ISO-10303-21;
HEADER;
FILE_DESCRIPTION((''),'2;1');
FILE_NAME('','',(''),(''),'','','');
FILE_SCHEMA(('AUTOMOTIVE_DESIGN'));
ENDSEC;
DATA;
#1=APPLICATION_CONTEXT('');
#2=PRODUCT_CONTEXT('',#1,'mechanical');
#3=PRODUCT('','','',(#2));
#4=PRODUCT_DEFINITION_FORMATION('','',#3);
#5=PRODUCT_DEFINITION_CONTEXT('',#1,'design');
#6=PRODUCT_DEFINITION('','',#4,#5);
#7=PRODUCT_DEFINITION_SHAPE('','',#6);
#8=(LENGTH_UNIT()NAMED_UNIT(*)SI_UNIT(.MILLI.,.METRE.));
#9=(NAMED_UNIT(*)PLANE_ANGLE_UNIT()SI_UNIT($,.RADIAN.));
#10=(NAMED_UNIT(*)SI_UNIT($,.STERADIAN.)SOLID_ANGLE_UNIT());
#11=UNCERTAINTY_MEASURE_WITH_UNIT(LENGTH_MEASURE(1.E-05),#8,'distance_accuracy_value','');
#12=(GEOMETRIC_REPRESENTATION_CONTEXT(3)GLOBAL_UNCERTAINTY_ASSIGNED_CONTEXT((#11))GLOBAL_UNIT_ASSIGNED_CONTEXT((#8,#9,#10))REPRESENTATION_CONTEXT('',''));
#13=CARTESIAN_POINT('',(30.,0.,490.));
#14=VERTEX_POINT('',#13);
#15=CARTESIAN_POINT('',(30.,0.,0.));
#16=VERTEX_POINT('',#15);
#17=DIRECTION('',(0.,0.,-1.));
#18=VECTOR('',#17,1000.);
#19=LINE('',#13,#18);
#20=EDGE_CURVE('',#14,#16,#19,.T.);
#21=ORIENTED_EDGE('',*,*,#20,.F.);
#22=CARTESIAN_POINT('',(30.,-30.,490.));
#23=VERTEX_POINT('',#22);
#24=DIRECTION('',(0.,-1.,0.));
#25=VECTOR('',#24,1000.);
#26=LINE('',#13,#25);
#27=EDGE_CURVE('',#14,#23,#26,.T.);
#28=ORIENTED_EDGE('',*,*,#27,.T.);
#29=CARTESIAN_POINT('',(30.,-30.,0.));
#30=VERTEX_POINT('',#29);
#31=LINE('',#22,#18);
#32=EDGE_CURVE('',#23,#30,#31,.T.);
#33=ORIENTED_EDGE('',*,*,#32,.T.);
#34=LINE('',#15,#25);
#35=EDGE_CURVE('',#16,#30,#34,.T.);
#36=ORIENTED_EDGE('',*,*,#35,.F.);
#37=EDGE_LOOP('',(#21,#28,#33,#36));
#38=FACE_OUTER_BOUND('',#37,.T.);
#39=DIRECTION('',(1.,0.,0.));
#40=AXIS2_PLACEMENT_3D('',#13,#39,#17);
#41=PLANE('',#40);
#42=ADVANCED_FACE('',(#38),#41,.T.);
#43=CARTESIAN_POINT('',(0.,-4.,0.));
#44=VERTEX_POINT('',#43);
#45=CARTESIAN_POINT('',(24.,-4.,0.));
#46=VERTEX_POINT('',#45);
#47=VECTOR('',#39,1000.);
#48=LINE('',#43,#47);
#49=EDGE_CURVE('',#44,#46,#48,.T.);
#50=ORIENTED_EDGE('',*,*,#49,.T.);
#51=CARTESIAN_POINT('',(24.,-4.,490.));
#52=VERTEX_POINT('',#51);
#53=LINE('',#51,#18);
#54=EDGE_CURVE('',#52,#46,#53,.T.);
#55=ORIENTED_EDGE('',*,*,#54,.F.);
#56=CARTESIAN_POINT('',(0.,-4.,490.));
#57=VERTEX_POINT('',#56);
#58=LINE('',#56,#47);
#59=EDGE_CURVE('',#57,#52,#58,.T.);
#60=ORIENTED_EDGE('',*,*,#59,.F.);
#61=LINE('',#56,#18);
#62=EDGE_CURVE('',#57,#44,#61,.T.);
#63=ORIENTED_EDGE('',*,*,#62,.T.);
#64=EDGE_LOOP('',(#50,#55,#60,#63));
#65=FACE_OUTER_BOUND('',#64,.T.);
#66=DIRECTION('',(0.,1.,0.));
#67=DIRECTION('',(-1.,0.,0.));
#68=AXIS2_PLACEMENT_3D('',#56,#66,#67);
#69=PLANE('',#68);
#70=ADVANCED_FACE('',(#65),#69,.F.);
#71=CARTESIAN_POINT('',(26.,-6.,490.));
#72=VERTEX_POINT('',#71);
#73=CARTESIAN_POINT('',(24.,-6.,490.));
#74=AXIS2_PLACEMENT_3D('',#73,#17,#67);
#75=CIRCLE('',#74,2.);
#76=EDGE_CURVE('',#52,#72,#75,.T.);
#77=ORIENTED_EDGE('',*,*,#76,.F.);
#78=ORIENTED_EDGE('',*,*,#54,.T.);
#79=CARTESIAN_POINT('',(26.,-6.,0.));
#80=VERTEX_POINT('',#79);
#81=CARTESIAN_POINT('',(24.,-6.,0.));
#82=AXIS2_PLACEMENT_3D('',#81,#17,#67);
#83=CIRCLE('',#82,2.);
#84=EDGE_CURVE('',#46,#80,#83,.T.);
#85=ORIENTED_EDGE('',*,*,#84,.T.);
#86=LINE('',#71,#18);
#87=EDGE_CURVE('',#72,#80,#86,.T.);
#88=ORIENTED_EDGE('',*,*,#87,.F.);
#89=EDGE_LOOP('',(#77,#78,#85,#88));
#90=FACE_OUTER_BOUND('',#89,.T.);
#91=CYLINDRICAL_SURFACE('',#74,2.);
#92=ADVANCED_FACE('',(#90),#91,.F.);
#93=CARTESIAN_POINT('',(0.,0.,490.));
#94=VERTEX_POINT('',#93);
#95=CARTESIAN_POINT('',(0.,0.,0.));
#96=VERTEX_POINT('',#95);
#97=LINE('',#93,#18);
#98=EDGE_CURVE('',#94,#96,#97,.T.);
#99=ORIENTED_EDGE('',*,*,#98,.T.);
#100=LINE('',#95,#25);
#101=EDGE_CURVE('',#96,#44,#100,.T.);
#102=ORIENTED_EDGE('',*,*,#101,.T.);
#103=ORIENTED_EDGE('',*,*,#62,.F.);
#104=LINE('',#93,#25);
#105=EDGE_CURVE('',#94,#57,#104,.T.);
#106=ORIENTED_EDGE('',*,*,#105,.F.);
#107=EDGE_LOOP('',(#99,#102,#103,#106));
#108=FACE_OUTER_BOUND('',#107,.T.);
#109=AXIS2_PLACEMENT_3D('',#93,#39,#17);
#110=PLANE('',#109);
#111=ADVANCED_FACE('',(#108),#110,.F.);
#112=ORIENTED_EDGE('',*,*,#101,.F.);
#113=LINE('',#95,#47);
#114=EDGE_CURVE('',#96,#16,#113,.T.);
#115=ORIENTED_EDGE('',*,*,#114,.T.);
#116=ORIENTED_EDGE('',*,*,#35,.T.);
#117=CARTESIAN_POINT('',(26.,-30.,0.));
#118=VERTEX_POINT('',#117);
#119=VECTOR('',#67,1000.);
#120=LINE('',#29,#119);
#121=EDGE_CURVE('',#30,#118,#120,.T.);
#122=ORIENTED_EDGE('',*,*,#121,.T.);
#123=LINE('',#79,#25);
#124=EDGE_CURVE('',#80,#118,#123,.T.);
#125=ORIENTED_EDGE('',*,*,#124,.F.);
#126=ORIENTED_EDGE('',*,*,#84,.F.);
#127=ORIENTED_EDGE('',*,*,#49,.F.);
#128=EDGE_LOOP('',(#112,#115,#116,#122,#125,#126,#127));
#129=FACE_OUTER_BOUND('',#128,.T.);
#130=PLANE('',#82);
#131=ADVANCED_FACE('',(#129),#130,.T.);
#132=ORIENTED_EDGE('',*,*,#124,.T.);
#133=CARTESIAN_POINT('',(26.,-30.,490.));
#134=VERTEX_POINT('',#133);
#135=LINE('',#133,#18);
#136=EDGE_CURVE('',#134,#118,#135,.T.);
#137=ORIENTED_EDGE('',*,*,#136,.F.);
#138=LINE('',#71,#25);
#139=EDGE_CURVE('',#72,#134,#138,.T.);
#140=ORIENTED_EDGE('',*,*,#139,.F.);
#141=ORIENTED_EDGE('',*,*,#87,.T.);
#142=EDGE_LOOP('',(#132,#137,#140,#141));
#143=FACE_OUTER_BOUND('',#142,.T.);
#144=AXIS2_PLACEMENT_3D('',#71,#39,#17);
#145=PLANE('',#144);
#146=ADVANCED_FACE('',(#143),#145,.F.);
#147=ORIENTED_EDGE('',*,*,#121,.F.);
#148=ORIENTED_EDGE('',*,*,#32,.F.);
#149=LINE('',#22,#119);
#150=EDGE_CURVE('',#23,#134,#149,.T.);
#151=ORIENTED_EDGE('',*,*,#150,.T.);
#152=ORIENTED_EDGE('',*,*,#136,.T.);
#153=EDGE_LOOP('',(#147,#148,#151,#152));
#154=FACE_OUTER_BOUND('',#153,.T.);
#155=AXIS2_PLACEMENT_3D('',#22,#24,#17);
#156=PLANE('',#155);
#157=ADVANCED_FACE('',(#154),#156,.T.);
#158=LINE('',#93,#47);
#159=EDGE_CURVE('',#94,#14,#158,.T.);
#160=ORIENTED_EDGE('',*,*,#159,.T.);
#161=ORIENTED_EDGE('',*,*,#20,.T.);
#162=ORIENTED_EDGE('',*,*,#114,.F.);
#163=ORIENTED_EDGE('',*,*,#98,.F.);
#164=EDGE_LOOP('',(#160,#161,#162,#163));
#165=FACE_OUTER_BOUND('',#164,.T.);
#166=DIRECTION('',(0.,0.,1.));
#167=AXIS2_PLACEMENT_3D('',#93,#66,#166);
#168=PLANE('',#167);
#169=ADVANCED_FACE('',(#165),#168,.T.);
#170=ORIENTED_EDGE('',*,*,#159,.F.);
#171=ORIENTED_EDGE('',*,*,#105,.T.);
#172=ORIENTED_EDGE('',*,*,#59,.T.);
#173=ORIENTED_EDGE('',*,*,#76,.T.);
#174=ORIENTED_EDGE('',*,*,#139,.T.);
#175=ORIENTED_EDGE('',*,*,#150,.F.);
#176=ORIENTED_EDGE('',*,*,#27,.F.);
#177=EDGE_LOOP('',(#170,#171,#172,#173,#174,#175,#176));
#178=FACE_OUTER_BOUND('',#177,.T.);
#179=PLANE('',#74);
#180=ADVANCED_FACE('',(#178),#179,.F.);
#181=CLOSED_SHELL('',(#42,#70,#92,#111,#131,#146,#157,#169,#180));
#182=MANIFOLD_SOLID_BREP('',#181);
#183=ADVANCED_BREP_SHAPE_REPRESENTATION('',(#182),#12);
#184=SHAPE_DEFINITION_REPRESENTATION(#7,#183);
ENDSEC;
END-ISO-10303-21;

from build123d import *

# Parameters (mm, degrees)
BOSS_EXTRUDE1_DEPTH = 490


with BuildPart() as part:
    # Sketch1 → Boss-Extrude1 (new body)
    with BuildSketch(Plane.XY):
        with BuildLine():
            Line((0, 0), (30, 0))
            Line((30, 0), (30, -30))
            Line((30, -30), (26, -30))
            Line((26, -30), (26, -6))
            ThreePointArc((26, -6), (25.414213562, -4.585786438), (24, -4))
            Line((24, -4), (0, -4))
            Line((0, -4), (0, 0))
        make_face()
    extrude(amount=BOSS_EXTRUDE1_DEPTH)


solid = part.part
